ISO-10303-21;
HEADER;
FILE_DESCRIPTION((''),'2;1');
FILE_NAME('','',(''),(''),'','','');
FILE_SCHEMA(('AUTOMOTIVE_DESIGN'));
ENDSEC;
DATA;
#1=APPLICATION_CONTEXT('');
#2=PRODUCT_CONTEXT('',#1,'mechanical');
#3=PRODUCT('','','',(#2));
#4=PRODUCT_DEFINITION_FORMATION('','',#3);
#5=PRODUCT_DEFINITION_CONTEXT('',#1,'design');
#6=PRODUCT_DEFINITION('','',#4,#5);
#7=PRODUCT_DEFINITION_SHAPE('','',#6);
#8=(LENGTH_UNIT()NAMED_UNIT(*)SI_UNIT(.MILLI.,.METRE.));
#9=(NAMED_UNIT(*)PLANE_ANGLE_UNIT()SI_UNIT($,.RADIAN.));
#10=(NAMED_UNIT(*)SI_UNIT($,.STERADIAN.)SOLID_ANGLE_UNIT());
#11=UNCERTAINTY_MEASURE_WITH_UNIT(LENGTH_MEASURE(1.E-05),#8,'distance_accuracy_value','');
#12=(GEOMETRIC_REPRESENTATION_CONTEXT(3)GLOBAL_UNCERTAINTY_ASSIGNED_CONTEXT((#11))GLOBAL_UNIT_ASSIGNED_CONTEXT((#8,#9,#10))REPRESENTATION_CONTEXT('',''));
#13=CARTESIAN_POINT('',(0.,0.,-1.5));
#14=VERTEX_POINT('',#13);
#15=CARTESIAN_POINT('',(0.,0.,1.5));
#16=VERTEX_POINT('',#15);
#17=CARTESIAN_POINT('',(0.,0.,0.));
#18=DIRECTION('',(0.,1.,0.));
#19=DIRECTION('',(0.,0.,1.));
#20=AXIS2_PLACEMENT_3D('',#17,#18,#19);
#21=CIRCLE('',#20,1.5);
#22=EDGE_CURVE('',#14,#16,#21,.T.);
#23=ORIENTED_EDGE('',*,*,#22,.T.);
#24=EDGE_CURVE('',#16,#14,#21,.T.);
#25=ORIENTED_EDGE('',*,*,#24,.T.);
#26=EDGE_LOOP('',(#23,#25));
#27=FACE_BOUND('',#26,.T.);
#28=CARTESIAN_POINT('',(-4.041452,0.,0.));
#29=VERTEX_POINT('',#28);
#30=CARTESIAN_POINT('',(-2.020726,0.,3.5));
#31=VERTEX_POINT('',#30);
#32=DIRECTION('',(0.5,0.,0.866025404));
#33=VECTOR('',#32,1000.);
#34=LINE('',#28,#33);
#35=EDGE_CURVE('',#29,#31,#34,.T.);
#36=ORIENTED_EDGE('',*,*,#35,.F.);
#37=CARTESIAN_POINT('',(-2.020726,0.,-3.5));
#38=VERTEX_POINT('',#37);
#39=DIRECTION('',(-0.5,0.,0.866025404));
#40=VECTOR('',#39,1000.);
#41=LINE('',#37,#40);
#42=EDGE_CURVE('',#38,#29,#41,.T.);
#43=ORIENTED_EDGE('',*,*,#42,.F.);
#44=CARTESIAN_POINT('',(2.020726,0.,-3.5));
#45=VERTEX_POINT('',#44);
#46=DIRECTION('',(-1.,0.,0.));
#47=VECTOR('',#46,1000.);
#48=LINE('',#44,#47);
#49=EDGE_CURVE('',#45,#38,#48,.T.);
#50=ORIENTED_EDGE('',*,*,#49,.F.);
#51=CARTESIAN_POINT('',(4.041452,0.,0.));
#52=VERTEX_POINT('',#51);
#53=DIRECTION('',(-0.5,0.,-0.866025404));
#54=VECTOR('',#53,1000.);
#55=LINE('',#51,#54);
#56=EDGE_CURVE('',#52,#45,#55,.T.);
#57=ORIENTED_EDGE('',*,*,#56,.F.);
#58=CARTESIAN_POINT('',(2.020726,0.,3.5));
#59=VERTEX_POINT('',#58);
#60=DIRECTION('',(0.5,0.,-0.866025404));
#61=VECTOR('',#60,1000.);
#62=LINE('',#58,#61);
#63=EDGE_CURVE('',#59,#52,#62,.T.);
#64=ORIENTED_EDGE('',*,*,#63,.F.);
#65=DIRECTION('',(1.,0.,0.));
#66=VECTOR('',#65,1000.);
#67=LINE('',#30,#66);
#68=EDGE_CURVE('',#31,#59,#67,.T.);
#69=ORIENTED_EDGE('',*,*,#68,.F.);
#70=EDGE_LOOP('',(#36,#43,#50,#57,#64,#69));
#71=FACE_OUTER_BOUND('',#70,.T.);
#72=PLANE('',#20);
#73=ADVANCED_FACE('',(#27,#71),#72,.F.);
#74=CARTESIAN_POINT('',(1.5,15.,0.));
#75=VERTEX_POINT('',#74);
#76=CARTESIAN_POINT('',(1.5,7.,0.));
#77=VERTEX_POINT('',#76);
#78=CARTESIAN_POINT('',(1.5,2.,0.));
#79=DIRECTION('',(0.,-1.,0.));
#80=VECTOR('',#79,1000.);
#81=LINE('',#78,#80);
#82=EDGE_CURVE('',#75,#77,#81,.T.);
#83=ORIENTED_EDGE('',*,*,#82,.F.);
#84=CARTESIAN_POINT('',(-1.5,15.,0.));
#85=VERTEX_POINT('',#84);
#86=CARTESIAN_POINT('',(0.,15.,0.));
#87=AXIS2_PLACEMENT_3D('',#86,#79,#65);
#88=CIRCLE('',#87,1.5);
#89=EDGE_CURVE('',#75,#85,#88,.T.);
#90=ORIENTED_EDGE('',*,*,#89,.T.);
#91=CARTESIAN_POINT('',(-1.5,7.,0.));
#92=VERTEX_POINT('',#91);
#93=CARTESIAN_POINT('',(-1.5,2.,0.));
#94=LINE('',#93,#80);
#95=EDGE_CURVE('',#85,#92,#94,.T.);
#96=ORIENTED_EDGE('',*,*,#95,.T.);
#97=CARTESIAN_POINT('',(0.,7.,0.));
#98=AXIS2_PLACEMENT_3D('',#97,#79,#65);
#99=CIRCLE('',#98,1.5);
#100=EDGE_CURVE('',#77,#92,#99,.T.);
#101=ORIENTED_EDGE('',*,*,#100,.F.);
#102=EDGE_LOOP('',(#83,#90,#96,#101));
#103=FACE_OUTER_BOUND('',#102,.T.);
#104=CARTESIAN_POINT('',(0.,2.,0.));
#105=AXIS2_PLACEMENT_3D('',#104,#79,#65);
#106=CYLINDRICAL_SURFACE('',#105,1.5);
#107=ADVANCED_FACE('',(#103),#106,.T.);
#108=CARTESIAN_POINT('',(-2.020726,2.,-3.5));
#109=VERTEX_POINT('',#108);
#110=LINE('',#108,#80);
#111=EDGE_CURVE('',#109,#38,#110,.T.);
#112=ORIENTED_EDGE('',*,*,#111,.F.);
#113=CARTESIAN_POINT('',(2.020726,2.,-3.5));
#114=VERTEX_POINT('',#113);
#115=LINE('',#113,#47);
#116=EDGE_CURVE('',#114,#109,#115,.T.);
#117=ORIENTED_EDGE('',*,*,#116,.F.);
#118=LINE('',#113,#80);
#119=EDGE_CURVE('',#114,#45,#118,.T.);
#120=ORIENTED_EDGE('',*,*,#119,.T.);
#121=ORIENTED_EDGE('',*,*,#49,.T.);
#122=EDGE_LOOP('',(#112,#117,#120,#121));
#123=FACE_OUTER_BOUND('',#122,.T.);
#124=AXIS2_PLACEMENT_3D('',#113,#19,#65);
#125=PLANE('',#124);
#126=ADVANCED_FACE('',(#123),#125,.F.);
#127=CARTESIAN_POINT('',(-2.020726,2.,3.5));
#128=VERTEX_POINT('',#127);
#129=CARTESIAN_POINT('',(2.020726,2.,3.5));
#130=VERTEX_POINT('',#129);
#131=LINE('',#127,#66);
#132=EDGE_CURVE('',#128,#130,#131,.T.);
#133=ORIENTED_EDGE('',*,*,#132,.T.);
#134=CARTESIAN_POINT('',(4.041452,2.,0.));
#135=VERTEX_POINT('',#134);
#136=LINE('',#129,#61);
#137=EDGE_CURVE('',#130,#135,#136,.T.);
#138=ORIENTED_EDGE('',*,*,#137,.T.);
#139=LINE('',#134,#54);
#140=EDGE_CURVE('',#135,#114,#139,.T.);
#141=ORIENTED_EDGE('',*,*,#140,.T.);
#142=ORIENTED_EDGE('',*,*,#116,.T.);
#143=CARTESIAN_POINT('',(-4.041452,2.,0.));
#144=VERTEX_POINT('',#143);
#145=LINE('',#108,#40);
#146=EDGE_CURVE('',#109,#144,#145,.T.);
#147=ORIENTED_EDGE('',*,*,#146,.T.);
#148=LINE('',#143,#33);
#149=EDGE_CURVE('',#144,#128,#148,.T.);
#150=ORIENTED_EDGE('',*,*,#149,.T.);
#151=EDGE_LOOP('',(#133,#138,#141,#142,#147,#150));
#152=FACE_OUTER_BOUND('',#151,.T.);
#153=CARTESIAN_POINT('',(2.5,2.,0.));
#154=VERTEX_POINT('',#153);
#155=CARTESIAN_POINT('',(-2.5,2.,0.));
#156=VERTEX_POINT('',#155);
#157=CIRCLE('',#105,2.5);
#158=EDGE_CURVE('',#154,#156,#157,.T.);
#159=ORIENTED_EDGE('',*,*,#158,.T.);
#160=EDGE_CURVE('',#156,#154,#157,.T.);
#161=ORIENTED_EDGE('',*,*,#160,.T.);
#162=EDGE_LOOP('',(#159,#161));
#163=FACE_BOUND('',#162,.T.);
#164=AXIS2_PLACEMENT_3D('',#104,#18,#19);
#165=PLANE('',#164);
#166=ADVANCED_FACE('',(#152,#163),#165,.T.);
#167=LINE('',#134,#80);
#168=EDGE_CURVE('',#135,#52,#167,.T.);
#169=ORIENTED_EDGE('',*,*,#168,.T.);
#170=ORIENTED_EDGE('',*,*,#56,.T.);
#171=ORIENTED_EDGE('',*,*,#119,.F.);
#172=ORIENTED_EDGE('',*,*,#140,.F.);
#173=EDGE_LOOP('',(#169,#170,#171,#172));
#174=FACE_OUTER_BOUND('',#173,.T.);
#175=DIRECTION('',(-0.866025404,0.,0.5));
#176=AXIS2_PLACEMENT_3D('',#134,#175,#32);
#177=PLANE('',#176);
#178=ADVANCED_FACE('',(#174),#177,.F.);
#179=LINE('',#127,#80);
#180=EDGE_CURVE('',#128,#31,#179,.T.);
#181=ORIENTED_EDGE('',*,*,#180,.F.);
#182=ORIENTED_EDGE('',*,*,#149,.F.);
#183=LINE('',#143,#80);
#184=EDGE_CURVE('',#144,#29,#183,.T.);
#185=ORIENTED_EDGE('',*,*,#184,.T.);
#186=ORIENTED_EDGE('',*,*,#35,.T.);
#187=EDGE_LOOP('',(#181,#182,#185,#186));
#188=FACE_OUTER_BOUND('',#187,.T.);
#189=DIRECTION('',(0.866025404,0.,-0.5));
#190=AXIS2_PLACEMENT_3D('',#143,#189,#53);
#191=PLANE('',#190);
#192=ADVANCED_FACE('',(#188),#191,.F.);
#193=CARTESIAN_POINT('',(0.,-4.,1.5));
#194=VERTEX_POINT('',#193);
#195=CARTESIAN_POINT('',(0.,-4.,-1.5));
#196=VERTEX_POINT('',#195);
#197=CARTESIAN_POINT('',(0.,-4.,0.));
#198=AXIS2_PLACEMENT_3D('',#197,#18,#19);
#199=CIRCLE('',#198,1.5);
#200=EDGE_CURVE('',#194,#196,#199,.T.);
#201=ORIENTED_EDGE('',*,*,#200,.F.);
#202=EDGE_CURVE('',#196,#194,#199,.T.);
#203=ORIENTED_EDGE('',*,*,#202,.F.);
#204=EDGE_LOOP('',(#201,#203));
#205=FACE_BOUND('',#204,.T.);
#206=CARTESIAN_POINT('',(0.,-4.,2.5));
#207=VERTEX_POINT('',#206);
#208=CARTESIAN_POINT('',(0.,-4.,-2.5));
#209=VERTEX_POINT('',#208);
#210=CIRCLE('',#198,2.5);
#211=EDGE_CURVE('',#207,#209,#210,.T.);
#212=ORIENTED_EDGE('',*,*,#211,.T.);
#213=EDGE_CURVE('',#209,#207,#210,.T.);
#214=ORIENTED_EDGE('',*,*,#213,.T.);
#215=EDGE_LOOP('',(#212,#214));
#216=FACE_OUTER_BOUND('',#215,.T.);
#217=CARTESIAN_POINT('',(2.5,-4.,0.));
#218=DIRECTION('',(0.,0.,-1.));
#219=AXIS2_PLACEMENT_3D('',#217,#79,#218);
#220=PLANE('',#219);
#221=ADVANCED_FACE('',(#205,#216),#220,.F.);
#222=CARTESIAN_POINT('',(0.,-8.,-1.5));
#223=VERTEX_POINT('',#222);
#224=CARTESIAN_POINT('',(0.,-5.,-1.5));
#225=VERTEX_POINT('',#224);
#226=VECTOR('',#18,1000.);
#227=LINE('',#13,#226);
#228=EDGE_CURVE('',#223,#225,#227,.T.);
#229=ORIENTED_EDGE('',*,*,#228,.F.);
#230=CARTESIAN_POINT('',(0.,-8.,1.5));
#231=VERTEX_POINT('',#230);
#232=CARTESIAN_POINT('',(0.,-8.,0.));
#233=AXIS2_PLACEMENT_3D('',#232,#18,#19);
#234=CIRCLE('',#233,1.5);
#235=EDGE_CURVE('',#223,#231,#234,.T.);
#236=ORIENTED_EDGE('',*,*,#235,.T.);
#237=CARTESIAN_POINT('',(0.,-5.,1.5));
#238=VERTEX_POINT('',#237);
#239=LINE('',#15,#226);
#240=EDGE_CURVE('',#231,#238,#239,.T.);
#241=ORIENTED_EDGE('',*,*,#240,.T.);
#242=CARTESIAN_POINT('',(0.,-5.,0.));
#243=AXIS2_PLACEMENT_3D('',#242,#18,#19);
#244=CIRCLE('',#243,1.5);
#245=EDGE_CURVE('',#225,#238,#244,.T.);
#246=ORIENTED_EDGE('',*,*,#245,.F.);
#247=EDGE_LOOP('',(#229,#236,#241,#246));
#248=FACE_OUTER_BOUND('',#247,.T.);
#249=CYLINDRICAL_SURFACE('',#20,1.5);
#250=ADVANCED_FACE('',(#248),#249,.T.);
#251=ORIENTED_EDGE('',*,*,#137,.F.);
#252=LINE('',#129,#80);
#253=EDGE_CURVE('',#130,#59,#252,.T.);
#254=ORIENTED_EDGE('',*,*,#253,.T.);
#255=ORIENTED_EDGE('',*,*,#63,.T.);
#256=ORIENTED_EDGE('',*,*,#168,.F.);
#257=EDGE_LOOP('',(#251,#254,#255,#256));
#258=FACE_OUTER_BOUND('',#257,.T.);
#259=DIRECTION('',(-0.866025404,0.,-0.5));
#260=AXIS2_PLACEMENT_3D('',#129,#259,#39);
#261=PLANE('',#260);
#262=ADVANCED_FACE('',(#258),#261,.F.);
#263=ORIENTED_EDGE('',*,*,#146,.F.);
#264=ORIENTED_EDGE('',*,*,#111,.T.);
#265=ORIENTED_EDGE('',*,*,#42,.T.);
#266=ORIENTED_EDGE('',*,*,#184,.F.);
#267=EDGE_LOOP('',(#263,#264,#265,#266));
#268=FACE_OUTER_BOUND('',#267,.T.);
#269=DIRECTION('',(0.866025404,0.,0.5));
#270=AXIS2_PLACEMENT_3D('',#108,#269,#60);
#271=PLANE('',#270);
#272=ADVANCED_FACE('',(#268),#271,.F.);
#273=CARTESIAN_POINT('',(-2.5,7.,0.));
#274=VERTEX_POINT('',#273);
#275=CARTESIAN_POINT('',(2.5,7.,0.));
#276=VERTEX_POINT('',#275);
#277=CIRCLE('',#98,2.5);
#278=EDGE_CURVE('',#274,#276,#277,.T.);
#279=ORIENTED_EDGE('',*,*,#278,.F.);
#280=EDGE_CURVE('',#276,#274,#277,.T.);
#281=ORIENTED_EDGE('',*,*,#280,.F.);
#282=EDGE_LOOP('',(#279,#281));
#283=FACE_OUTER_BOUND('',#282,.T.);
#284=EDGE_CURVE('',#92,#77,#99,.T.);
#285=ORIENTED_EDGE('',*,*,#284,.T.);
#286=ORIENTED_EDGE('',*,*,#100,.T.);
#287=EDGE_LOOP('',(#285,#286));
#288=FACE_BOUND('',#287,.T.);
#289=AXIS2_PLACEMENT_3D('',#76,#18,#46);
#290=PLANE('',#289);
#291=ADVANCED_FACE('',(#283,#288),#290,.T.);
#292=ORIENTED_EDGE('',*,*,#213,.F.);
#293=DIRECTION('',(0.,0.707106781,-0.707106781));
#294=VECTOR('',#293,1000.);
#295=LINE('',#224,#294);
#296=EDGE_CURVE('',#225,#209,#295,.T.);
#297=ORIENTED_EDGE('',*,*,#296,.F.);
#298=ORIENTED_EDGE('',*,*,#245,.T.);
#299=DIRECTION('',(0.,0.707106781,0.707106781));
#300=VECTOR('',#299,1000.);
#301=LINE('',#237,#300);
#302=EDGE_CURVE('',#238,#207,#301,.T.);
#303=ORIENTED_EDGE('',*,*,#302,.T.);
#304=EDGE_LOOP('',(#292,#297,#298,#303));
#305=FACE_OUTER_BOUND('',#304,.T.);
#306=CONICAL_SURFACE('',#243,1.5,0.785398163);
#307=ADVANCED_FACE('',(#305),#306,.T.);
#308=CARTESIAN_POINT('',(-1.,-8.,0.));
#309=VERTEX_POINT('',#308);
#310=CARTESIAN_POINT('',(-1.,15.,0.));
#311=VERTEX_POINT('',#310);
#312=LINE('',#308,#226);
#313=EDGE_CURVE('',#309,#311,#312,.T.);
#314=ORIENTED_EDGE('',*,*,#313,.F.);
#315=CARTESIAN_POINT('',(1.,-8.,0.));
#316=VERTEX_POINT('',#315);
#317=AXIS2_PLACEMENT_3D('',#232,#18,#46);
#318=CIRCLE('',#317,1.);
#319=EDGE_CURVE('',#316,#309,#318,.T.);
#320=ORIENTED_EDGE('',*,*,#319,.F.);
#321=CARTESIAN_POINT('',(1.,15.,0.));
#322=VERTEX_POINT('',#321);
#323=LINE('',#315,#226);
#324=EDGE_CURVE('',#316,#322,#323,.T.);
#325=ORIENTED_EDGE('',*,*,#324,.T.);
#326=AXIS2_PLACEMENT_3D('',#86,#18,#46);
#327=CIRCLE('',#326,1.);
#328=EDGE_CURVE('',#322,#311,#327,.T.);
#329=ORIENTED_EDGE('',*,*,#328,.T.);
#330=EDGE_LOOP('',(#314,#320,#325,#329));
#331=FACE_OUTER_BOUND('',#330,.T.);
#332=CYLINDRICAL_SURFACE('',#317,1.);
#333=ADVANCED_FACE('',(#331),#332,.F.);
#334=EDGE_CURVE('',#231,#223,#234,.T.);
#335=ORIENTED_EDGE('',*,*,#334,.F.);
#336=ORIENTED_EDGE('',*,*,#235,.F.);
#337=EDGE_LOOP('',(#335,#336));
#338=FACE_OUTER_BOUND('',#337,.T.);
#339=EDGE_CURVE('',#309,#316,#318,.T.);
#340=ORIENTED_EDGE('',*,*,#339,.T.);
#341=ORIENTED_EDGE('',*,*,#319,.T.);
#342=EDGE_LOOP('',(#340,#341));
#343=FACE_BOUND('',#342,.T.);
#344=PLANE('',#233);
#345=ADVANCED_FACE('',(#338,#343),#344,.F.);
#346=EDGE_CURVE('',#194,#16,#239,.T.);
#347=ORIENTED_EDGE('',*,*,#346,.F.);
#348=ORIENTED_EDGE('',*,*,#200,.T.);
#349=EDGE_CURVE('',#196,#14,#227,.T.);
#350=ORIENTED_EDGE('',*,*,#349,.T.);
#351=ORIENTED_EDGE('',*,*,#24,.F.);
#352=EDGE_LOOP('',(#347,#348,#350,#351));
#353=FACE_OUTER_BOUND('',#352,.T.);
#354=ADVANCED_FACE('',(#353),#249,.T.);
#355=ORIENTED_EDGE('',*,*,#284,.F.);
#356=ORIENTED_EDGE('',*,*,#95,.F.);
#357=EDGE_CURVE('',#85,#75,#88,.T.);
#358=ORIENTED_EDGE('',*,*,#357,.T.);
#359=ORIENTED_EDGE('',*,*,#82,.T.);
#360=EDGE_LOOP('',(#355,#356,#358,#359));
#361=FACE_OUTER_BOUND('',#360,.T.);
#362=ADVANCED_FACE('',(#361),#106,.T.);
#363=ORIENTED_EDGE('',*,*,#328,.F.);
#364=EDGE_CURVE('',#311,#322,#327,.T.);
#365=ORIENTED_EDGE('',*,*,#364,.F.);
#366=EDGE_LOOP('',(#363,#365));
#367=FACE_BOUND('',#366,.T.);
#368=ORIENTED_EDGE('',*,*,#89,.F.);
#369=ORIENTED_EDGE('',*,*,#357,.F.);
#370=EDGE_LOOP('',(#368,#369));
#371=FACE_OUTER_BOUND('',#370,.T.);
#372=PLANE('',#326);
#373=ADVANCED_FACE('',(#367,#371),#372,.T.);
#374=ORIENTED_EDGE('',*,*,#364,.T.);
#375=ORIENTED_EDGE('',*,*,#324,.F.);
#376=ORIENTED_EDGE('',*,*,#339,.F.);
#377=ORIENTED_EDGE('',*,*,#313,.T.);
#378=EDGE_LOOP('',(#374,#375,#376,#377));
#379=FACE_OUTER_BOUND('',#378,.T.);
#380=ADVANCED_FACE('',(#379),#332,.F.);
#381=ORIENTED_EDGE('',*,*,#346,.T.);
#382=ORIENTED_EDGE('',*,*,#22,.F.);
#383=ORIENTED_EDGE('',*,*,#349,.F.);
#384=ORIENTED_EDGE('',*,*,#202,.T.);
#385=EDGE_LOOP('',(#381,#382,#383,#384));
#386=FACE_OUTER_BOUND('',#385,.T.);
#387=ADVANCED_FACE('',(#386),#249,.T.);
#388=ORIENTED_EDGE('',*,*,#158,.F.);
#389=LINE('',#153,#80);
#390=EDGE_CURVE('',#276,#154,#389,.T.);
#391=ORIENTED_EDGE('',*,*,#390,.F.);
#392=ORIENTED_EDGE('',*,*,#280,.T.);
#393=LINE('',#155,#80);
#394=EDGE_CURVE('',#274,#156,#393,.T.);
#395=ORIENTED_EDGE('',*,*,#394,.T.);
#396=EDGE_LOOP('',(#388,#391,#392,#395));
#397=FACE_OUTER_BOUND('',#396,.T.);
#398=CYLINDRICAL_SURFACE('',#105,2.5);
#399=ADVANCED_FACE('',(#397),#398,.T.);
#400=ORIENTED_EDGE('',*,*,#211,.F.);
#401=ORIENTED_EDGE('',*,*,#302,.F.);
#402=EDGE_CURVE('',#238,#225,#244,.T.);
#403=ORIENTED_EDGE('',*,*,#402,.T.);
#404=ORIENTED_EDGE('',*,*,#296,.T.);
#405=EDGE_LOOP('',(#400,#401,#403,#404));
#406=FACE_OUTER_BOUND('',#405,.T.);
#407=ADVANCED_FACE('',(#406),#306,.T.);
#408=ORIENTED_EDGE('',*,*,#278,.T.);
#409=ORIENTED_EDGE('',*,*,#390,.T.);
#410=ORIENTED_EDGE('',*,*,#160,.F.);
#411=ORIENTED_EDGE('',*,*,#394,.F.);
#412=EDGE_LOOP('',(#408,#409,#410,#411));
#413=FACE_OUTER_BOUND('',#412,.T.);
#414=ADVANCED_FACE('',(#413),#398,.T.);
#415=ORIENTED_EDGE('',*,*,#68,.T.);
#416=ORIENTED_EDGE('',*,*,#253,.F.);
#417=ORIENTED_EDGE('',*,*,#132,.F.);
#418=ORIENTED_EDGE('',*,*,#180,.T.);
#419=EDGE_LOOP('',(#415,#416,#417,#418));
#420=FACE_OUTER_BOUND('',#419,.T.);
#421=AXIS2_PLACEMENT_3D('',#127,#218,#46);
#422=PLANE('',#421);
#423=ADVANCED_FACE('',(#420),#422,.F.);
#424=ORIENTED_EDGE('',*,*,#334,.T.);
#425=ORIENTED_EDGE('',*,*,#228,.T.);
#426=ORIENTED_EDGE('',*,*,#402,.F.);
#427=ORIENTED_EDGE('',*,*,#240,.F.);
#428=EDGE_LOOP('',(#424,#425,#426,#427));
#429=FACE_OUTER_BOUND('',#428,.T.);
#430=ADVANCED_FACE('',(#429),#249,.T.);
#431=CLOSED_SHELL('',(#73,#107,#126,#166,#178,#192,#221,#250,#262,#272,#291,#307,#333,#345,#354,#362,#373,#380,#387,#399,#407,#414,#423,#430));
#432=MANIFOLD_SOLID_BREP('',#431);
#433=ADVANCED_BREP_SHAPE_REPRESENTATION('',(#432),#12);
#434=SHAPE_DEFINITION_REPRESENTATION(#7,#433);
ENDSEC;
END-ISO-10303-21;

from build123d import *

# Parameters (mm, degrees)
HEX_7AF_DEPTH     = 2
BORE_PROFILE_2_R  = 1
FUEL_BORE_2_DEPTH = 24.613202522


with BuildPart() as part:
    # Lower Spigot Profile → Lower Spigot and Collar (revolve)
    with BuildSketch(Plane.XY, mode=Mode.PRIVATE) as lower_spigot_and_collar_sk:
        Polygon((0, 0), (0, -8), (1.5, -8), (1.5, -5), (2.5, -4), (1.5, -4), (1.5, 0), align=None)
    revolve(lower_spigot_and_collar_sk.sketch.rotate(Axis((0, 0, 0), (0, -1, 0)), 90), axis=Axis((0, 0, 0), (0, -1, 0)))

    # Hex Profile 7AF → Hex 7AF (add)
    with BuildSketch(Plane(origin=(0, 0, 0), x_dir=(1, 0, 0), z_dir=(0, 1, 0))):
        Polygon((4.041451884, 0), (2.020725942, 3.5), (-2.020725942, 3.5), (-4.041451884, 0), (-2.020725942, -3.5), (2.020725942, -3.5), align=None)
    extrude(amount=HEX_7AF_DEPTH)

    # Upper Pipe Profile → Upper Pipe (revolve)
    with BuildSketch(Plane.XY):
        Polygon((0, 2), (0, 15), (1.5, 15), (1.5, 7), (2.5, 7), (2.5, 2), align=None)
    revolve(axis=Axis((0, 2, 0), (0, 1, 0)))

    # Bore Profile Ø2 → Fuel Bore Ø2 (cut, through all)
    with BuildSketch(Plane(origin=(0, 15, 0), x_dir=(1, 0, 0), z_dir=(0, 1, 0))):
        with Locations(Location((0, 0, 0), (0, 0, 180))):
            Circle(BORE_PROFILE_2_R)
    extrude(amount=-FUEL_BORE_2_DEPTH, mode=Mode.SUBTRACT)


solid = part.part
